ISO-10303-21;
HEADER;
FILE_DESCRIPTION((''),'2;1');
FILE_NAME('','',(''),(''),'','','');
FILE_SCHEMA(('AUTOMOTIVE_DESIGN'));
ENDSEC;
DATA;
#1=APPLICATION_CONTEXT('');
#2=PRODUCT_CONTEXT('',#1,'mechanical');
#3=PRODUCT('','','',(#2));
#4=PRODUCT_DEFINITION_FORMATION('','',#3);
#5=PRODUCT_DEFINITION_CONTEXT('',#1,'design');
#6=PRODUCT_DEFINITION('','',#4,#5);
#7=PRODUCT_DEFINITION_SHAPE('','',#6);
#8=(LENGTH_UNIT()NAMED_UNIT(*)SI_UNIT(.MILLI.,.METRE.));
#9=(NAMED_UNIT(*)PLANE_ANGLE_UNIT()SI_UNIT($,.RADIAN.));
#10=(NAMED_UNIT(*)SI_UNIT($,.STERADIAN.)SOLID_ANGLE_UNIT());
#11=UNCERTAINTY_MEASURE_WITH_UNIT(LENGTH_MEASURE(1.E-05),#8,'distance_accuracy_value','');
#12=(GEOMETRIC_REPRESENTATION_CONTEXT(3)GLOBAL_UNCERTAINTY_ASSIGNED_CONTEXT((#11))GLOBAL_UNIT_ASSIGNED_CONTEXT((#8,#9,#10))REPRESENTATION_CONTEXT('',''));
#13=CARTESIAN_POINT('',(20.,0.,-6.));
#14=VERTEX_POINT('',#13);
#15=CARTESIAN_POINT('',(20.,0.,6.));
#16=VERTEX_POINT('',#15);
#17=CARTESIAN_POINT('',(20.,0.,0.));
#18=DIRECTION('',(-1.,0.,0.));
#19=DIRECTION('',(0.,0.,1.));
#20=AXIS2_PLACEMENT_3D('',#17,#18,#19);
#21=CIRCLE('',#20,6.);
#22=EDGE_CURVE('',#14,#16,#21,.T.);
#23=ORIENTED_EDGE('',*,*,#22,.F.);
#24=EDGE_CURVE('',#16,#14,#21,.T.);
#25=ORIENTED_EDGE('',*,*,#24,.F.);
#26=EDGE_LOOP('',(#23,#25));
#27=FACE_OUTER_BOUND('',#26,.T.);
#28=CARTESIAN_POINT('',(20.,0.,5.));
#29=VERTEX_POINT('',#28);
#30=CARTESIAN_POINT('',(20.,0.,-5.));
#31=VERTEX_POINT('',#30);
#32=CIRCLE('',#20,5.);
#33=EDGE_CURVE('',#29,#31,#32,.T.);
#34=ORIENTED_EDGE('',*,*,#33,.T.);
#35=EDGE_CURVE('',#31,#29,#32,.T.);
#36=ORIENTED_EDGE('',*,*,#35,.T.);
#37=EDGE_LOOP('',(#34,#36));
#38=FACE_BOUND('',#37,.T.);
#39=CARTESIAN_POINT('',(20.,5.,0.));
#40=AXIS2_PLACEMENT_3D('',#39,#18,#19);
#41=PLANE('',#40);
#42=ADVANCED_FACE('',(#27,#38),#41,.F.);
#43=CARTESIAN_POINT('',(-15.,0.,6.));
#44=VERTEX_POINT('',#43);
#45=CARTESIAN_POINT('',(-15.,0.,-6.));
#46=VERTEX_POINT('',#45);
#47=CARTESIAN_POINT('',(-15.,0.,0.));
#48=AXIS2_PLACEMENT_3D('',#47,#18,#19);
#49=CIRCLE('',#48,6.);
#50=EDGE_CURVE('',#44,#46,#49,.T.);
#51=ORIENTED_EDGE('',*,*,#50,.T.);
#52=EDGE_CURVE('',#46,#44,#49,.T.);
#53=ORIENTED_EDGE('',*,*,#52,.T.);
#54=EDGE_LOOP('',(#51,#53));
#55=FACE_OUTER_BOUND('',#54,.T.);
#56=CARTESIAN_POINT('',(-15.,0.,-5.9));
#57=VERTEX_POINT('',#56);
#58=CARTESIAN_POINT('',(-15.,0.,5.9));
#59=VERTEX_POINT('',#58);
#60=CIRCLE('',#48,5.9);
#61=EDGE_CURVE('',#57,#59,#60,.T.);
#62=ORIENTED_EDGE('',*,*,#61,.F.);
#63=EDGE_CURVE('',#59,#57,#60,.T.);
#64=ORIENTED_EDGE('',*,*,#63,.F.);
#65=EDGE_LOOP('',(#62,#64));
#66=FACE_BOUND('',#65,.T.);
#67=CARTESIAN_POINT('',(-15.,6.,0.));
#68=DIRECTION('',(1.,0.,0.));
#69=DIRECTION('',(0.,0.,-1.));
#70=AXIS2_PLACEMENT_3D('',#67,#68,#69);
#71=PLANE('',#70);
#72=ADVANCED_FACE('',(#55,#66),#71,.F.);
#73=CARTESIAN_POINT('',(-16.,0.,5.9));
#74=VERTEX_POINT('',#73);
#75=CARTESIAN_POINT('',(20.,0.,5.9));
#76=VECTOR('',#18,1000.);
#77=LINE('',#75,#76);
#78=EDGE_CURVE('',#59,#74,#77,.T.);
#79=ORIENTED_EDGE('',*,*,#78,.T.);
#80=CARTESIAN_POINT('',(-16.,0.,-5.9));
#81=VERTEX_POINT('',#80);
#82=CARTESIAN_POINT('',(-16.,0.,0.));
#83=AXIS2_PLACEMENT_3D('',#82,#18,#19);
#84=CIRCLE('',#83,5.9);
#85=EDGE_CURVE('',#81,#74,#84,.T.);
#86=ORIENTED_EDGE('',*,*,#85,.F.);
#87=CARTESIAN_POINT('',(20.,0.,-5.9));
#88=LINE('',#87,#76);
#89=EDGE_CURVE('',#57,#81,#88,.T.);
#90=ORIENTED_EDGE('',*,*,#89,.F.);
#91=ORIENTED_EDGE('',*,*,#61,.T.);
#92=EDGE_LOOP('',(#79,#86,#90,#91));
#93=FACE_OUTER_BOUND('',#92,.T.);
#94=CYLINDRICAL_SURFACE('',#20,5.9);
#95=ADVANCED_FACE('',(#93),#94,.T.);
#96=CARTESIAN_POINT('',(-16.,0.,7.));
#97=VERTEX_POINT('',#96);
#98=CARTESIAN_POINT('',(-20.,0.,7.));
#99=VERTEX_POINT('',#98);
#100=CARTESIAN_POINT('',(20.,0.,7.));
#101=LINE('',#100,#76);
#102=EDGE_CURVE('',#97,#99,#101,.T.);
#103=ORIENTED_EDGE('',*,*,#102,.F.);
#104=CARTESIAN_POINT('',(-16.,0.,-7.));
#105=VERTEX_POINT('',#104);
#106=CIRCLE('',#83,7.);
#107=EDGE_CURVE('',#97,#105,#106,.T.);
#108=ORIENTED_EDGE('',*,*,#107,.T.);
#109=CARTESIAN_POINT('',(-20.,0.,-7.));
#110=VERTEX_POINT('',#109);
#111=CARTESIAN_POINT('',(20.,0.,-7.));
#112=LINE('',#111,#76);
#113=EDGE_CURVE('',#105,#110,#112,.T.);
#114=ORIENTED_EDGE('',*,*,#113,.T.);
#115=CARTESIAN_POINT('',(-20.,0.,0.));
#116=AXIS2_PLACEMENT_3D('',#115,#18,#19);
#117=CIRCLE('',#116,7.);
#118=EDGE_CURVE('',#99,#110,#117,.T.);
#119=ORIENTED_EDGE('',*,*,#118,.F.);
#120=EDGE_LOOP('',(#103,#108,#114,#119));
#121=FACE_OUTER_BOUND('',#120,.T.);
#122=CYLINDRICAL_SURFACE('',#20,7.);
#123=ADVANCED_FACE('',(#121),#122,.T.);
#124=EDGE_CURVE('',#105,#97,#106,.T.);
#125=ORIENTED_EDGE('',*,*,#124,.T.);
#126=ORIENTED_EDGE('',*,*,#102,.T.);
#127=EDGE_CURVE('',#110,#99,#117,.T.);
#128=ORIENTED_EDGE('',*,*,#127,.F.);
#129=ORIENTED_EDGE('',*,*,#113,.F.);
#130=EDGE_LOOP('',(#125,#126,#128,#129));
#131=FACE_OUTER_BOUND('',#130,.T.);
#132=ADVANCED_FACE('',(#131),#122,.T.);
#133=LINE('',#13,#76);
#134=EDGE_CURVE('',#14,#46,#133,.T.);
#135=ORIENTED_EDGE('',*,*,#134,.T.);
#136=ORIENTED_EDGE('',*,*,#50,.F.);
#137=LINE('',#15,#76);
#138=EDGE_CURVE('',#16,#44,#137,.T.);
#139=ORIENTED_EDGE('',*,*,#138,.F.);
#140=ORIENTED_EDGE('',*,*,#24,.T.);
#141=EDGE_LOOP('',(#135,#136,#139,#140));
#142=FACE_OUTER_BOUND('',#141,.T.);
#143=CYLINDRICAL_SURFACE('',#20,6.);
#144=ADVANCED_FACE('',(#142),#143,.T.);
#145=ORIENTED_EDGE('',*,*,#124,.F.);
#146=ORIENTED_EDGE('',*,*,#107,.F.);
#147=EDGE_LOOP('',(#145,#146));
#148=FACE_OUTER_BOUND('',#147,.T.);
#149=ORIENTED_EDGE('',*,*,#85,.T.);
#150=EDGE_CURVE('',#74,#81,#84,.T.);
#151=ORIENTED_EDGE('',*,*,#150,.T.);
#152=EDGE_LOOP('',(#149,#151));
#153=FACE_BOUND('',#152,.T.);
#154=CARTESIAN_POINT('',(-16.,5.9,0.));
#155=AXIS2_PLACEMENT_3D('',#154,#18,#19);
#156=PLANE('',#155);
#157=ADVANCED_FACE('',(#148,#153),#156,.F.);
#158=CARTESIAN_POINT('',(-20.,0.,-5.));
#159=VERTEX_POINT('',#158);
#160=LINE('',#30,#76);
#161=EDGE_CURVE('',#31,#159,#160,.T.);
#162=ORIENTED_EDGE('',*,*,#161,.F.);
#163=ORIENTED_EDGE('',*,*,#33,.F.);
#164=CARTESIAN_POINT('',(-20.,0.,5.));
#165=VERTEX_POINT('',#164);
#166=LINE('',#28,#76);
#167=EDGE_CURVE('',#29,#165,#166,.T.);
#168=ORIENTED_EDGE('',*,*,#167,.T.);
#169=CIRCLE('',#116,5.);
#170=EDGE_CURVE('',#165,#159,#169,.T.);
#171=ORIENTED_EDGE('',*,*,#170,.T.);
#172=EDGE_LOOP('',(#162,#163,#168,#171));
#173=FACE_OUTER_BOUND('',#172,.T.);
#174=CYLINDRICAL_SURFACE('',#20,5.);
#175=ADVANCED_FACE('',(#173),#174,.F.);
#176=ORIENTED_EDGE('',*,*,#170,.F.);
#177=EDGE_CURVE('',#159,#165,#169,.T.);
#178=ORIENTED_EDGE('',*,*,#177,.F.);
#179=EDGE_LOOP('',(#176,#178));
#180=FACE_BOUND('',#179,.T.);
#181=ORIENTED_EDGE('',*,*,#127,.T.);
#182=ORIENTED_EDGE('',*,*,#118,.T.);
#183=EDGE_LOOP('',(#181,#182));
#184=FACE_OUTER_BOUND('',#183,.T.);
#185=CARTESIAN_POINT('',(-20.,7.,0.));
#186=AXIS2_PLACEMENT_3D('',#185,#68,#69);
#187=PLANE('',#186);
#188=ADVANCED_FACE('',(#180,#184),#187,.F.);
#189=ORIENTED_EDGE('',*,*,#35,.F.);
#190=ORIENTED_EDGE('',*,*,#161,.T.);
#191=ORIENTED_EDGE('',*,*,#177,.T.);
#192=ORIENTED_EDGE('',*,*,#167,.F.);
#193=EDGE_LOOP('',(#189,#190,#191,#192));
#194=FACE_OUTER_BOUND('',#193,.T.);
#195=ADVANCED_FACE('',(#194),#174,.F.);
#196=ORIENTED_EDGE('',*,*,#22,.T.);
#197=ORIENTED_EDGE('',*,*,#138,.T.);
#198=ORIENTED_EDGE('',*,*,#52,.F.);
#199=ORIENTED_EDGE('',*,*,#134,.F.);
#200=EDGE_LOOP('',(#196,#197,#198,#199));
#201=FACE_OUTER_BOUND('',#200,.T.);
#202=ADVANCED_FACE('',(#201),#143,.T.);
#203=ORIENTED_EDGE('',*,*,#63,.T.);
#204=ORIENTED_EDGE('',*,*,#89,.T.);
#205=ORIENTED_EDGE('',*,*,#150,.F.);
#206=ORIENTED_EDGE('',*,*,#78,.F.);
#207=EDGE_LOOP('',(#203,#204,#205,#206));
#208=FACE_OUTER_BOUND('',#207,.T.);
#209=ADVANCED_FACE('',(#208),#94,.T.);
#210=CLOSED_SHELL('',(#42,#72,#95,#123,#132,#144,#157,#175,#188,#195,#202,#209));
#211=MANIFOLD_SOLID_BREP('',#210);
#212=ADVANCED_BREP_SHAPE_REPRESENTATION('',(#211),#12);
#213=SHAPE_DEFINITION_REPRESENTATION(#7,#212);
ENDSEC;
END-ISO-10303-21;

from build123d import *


with BuildPart() as part:
    # Sketch1 → Revolve1 (revolve)
    with BuildSketch(Plane.XY, mode=Mode.PRIVATE) as revolve1_sk:
        Polygon((-20, 7), (-20, 5), (20, 5), (20, 6), (-15, 6), (-15, 5.9), (-16, 5.9), (-16, 7), align=None)
    revolve(revolve1_sk.sketch.rotate(Axis((20, 0, 0), (-1, 0, 0)), 270), axis=Axis((20, 0, 0), (-1, 0, 0)))


solid = part.part
